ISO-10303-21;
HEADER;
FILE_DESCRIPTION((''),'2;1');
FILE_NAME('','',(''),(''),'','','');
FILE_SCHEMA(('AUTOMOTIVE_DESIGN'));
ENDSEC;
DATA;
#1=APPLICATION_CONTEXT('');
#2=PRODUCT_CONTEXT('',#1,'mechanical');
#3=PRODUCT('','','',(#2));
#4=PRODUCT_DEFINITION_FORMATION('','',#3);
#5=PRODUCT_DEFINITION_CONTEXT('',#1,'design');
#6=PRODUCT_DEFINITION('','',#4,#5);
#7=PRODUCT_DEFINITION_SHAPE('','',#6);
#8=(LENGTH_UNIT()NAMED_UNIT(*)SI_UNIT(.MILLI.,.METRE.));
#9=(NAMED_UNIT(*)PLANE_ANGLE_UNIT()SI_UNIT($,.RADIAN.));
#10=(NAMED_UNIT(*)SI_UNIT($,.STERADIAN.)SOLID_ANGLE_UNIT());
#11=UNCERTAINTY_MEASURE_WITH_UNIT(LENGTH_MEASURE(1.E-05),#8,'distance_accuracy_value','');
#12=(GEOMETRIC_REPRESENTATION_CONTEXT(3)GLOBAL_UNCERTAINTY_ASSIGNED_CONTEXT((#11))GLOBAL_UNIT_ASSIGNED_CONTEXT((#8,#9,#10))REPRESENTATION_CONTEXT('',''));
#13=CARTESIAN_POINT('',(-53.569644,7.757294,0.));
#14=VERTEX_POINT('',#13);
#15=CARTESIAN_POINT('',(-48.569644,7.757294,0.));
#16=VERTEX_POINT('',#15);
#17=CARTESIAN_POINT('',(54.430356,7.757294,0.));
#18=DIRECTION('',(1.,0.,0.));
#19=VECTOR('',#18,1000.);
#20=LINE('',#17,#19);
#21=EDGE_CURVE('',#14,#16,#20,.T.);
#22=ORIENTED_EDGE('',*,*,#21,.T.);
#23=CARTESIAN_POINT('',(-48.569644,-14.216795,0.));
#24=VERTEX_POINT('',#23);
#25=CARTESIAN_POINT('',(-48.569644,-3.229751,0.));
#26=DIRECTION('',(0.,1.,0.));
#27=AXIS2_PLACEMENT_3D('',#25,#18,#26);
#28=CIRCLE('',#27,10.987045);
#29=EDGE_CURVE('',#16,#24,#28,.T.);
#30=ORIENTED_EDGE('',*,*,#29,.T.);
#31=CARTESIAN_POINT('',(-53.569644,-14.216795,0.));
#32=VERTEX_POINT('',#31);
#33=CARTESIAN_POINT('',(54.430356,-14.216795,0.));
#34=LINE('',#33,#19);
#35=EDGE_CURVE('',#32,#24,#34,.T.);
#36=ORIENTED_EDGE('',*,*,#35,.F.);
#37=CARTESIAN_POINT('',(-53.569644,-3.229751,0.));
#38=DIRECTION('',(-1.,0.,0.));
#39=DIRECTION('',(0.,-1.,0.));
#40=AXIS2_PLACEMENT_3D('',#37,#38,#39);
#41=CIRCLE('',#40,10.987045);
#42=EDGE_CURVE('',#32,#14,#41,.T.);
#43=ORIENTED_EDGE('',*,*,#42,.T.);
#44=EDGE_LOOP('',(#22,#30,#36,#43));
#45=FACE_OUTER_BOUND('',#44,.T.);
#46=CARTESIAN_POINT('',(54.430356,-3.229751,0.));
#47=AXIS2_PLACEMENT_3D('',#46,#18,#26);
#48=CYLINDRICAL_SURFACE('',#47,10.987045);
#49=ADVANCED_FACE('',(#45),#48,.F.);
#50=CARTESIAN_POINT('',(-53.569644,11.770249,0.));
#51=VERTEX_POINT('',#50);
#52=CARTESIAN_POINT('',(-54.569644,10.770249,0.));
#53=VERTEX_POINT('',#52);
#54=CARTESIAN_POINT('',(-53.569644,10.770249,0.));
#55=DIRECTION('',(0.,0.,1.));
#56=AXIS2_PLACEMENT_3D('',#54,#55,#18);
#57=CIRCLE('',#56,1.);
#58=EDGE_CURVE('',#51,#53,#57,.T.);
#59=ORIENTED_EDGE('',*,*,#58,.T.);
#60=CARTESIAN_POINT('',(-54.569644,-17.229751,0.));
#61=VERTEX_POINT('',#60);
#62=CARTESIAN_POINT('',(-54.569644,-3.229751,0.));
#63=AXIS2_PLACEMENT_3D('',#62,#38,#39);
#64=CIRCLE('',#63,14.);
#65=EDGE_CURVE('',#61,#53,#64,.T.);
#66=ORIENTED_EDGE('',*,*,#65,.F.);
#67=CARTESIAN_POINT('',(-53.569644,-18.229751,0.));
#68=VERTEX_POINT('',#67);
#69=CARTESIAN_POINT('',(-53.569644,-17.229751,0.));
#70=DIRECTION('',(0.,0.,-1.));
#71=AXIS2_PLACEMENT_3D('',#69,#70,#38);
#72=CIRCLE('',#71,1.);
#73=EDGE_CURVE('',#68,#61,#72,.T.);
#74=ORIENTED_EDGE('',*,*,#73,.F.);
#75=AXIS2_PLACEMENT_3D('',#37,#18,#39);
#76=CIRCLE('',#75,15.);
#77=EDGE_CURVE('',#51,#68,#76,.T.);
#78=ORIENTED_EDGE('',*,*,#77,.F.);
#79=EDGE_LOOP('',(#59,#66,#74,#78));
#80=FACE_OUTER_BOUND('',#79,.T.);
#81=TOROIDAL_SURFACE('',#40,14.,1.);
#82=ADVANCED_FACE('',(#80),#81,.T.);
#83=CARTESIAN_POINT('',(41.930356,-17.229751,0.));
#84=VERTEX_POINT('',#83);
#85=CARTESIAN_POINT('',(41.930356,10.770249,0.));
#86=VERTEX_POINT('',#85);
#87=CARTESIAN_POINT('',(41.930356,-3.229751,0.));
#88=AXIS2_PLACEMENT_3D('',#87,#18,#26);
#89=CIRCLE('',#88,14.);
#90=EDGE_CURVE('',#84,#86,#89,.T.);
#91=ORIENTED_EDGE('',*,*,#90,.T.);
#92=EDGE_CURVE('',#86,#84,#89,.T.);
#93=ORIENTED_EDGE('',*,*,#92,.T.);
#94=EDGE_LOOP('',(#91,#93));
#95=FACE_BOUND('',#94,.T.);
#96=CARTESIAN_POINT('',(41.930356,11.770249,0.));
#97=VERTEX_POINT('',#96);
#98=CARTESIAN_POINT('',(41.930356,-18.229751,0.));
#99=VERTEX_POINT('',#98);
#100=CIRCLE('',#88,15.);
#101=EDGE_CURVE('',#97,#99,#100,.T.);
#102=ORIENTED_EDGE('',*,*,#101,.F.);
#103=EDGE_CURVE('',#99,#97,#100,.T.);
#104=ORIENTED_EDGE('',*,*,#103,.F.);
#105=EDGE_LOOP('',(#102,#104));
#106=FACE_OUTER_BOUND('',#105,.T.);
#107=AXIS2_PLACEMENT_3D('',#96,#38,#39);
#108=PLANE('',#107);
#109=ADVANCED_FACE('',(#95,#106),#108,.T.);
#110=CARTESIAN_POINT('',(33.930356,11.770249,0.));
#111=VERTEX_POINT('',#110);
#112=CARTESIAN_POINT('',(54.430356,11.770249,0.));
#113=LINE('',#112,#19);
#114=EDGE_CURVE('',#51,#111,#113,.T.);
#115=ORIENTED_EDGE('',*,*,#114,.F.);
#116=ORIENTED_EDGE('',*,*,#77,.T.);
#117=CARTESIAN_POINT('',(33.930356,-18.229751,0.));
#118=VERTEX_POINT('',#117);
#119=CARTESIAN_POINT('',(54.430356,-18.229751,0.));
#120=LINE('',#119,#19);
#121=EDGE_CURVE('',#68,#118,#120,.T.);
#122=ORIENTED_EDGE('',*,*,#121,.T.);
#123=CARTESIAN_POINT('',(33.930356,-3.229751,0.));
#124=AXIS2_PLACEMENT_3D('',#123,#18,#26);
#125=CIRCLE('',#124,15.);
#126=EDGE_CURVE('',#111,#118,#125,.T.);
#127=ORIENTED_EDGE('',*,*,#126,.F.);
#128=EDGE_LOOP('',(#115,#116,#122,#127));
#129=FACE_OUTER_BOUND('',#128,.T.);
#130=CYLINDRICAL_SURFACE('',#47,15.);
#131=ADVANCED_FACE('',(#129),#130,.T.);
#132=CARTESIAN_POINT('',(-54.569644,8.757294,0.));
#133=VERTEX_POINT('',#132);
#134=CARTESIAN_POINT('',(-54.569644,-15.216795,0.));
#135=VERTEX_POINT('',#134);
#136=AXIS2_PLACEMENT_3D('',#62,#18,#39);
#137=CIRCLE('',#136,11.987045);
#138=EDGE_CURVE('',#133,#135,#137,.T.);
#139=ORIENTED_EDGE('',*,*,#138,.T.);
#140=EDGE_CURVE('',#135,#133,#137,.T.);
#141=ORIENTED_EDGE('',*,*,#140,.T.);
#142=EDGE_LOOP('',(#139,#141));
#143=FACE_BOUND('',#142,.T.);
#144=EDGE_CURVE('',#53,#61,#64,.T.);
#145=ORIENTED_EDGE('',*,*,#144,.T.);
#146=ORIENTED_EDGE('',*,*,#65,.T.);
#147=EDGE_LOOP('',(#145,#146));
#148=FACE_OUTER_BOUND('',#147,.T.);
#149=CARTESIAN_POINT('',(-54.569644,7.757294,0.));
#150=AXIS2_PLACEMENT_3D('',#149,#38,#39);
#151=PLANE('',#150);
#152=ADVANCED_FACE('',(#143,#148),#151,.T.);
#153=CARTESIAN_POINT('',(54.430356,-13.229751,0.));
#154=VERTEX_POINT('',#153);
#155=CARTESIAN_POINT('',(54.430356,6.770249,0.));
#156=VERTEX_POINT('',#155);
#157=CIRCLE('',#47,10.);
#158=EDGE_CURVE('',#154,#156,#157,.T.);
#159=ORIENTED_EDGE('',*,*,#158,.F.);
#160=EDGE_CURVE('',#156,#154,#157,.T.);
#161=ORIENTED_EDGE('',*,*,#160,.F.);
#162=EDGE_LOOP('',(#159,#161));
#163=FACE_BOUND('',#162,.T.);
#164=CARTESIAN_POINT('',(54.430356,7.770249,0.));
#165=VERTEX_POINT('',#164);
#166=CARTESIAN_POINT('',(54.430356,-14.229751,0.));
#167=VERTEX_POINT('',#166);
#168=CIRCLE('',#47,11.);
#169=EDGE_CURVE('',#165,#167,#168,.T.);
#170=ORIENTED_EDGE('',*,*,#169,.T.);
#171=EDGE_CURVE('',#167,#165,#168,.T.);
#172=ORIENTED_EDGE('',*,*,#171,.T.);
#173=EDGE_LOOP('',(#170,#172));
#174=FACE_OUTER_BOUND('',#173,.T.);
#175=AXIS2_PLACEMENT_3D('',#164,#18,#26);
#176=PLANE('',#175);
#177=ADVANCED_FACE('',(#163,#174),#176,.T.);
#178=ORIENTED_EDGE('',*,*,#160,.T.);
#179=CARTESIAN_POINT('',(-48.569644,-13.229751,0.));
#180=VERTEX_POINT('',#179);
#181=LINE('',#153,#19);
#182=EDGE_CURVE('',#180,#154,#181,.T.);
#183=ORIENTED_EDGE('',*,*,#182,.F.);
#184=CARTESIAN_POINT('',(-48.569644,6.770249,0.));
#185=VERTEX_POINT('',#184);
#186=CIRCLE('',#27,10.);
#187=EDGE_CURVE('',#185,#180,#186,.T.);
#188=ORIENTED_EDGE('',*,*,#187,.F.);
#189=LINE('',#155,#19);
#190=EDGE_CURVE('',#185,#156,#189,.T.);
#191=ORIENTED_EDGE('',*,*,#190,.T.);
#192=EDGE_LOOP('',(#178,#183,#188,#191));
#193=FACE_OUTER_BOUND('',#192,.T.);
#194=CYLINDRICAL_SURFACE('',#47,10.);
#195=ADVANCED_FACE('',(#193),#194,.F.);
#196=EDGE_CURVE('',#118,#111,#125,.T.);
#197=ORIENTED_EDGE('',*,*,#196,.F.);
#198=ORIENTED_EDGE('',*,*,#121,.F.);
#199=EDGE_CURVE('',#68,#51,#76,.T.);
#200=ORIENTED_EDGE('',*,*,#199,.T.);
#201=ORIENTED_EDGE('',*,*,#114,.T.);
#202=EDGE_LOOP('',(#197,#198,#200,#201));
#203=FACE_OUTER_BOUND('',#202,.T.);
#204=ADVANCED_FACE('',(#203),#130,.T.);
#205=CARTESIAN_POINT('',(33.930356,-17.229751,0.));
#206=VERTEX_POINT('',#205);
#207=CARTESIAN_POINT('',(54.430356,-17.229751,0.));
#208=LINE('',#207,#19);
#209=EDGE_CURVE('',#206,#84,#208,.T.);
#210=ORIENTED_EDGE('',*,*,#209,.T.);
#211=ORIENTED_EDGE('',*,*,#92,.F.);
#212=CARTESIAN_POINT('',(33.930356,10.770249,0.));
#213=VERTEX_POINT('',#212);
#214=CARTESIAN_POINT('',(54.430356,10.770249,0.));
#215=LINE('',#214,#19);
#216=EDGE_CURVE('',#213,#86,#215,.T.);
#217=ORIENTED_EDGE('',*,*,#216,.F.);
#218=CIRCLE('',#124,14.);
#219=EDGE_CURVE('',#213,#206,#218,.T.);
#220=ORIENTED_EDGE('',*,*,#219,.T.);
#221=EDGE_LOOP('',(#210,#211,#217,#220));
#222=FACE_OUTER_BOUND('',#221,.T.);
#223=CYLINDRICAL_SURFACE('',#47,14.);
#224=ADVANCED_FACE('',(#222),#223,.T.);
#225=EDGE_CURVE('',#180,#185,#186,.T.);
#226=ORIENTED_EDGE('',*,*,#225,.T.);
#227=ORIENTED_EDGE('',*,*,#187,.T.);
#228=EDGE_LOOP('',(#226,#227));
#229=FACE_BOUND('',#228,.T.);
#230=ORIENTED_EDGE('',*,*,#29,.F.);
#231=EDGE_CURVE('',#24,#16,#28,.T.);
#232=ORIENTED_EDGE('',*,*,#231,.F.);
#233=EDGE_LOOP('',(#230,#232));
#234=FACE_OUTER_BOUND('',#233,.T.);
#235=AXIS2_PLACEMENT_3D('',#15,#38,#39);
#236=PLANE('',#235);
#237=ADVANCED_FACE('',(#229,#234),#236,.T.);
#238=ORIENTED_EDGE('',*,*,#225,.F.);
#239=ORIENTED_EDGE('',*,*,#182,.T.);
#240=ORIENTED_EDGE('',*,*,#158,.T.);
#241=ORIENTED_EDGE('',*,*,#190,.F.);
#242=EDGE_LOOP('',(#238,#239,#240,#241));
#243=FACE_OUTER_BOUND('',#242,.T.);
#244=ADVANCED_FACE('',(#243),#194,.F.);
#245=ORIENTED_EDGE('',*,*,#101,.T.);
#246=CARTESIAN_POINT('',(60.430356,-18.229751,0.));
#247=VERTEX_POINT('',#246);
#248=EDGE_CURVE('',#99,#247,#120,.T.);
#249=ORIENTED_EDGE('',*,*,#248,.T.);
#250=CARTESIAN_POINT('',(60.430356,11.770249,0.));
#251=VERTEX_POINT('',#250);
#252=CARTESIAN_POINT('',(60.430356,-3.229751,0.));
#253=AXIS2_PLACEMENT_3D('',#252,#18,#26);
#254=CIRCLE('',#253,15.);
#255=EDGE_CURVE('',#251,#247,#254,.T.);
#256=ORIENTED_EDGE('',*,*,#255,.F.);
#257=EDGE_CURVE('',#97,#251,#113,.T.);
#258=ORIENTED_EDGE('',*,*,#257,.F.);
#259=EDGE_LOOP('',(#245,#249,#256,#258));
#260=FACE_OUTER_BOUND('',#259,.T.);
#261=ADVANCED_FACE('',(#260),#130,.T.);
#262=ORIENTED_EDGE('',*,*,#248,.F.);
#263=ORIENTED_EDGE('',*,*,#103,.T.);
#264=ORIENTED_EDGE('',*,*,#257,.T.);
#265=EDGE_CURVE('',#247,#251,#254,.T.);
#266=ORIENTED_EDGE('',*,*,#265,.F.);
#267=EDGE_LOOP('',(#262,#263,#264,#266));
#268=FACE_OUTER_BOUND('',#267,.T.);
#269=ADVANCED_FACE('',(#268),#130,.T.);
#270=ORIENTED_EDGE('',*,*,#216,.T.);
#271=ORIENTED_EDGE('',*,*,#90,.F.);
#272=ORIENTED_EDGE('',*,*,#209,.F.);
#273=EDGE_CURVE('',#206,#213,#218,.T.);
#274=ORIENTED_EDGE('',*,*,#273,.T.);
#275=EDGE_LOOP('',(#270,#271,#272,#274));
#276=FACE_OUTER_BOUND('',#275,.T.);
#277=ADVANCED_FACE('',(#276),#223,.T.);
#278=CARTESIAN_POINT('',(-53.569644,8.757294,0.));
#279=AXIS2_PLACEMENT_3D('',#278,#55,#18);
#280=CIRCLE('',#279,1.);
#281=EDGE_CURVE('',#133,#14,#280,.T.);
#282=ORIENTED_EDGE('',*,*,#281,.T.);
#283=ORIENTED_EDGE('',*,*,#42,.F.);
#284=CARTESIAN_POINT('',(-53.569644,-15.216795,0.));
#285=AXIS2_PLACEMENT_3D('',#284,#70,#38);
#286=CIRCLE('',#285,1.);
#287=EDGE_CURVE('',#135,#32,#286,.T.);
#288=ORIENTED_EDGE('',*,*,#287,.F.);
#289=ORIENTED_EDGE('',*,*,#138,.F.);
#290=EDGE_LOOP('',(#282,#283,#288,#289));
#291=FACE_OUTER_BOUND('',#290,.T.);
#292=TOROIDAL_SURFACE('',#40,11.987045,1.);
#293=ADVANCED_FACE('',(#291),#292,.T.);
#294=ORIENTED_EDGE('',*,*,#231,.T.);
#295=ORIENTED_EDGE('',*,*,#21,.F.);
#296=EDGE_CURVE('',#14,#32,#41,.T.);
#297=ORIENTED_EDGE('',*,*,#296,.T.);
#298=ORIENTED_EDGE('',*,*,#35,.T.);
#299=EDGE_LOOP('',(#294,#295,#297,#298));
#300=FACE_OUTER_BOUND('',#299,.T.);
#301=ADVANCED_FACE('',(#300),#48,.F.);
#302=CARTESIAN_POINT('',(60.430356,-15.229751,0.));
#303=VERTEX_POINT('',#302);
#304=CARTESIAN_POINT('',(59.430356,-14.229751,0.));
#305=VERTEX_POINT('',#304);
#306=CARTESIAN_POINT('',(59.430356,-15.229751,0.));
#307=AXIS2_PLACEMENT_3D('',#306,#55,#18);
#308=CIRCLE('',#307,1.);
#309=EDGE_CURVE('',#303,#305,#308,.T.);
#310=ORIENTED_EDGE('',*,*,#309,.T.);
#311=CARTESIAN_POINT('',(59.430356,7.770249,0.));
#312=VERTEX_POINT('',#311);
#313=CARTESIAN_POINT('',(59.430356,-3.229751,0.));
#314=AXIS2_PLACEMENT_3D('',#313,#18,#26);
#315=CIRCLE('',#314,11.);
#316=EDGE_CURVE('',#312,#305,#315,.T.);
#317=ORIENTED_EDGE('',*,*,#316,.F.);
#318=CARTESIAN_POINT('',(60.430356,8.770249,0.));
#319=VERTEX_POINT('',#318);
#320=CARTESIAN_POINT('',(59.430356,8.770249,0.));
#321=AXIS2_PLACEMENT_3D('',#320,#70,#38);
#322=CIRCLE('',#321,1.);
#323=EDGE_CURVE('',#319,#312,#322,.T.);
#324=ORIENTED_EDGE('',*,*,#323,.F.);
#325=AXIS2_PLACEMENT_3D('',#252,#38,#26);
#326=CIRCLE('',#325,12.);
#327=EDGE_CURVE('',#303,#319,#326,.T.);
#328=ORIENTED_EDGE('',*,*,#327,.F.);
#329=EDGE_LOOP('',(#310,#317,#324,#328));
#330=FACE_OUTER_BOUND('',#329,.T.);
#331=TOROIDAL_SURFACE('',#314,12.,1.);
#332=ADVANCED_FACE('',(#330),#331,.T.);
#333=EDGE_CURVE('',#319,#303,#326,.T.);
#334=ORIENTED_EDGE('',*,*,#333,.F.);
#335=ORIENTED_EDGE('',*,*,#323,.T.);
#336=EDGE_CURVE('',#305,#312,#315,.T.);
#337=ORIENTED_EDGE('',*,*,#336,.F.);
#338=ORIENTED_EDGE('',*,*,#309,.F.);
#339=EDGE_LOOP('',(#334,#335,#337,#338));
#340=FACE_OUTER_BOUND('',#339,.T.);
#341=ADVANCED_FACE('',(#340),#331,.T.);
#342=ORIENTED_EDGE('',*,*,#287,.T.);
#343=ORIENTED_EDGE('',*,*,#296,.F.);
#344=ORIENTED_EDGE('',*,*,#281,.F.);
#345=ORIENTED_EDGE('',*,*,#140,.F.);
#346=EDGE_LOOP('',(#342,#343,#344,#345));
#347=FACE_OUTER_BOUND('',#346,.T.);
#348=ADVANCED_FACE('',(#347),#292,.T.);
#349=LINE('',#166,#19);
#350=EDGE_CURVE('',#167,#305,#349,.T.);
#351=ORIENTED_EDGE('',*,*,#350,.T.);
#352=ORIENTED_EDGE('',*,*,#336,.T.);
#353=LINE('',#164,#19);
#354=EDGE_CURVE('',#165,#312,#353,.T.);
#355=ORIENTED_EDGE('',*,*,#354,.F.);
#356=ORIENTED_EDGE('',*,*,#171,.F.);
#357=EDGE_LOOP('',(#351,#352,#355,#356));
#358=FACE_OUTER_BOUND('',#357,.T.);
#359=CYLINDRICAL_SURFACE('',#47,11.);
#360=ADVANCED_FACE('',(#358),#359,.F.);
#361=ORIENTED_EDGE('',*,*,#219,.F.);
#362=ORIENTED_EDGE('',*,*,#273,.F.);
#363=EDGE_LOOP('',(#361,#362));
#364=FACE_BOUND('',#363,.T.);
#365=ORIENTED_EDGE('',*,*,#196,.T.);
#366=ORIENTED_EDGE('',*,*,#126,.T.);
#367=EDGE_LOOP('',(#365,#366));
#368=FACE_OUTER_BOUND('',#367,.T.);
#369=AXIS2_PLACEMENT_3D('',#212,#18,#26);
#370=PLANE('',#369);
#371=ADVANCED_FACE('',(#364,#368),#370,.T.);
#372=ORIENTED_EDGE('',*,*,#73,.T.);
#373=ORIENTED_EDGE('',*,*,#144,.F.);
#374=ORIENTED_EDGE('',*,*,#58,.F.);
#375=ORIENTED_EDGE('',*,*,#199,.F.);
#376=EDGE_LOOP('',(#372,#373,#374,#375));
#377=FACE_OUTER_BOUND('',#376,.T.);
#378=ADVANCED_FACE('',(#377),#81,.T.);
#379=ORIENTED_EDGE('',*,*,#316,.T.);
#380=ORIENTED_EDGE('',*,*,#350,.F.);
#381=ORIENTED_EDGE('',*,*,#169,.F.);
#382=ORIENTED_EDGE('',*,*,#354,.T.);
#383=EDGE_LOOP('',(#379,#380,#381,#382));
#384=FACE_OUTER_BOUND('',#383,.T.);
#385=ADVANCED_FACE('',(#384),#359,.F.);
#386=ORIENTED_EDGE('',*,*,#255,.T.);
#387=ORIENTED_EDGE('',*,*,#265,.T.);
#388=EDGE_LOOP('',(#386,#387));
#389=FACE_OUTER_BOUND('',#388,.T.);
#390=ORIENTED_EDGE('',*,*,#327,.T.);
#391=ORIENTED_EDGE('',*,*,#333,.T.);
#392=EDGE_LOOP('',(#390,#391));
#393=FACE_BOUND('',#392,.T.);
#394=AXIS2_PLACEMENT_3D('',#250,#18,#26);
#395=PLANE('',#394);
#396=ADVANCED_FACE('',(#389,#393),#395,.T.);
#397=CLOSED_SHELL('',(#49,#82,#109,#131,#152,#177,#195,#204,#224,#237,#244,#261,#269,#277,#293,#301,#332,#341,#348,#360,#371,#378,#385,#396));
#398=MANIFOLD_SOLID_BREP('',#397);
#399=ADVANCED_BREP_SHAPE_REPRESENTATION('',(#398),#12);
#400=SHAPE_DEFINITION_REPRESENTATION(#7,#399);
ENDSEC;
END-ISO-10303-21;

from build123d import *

# Parameters (mm, degrees)
FILLET1_R = 1


with BuildPart() as part:
    # Sketch1 → Revolve1 (revolve)
    with BuildSketch(Plane.XY):
        Polygon((-54.569644219, 7.757293726), (-54.569644219, 11.770249221), (33.930355781, 11.770249221), (33.930355781, 10.770249221), (41.930355781, 10.770249221), (41.930355781, 11.770249221), (60.430355781, 11.770249221), (60.430355781, 7.770249221), (54.430355781, 7.770249221), (54.430355781, 6.770249221), (-48.569644219, 6.770249221), (-48.569644219, 7.757293726), align=None)
    revolve(axis=Axis((54.430355781, -3.229750779, 0), (-1, 0, 0)))

    # Fillet1
    fillet1_edges = [part.edges().sort_by_distance(p)[0] for p in [
        (-54.569644219, -18.229750779, 0),
        (-54.569644219, -14.216795283, 0),
        (60.430355781, -14.229750779, 0),
    ]]
    fillet(fillet1_edges, radius=FILLET1_R)


solid = part.part
